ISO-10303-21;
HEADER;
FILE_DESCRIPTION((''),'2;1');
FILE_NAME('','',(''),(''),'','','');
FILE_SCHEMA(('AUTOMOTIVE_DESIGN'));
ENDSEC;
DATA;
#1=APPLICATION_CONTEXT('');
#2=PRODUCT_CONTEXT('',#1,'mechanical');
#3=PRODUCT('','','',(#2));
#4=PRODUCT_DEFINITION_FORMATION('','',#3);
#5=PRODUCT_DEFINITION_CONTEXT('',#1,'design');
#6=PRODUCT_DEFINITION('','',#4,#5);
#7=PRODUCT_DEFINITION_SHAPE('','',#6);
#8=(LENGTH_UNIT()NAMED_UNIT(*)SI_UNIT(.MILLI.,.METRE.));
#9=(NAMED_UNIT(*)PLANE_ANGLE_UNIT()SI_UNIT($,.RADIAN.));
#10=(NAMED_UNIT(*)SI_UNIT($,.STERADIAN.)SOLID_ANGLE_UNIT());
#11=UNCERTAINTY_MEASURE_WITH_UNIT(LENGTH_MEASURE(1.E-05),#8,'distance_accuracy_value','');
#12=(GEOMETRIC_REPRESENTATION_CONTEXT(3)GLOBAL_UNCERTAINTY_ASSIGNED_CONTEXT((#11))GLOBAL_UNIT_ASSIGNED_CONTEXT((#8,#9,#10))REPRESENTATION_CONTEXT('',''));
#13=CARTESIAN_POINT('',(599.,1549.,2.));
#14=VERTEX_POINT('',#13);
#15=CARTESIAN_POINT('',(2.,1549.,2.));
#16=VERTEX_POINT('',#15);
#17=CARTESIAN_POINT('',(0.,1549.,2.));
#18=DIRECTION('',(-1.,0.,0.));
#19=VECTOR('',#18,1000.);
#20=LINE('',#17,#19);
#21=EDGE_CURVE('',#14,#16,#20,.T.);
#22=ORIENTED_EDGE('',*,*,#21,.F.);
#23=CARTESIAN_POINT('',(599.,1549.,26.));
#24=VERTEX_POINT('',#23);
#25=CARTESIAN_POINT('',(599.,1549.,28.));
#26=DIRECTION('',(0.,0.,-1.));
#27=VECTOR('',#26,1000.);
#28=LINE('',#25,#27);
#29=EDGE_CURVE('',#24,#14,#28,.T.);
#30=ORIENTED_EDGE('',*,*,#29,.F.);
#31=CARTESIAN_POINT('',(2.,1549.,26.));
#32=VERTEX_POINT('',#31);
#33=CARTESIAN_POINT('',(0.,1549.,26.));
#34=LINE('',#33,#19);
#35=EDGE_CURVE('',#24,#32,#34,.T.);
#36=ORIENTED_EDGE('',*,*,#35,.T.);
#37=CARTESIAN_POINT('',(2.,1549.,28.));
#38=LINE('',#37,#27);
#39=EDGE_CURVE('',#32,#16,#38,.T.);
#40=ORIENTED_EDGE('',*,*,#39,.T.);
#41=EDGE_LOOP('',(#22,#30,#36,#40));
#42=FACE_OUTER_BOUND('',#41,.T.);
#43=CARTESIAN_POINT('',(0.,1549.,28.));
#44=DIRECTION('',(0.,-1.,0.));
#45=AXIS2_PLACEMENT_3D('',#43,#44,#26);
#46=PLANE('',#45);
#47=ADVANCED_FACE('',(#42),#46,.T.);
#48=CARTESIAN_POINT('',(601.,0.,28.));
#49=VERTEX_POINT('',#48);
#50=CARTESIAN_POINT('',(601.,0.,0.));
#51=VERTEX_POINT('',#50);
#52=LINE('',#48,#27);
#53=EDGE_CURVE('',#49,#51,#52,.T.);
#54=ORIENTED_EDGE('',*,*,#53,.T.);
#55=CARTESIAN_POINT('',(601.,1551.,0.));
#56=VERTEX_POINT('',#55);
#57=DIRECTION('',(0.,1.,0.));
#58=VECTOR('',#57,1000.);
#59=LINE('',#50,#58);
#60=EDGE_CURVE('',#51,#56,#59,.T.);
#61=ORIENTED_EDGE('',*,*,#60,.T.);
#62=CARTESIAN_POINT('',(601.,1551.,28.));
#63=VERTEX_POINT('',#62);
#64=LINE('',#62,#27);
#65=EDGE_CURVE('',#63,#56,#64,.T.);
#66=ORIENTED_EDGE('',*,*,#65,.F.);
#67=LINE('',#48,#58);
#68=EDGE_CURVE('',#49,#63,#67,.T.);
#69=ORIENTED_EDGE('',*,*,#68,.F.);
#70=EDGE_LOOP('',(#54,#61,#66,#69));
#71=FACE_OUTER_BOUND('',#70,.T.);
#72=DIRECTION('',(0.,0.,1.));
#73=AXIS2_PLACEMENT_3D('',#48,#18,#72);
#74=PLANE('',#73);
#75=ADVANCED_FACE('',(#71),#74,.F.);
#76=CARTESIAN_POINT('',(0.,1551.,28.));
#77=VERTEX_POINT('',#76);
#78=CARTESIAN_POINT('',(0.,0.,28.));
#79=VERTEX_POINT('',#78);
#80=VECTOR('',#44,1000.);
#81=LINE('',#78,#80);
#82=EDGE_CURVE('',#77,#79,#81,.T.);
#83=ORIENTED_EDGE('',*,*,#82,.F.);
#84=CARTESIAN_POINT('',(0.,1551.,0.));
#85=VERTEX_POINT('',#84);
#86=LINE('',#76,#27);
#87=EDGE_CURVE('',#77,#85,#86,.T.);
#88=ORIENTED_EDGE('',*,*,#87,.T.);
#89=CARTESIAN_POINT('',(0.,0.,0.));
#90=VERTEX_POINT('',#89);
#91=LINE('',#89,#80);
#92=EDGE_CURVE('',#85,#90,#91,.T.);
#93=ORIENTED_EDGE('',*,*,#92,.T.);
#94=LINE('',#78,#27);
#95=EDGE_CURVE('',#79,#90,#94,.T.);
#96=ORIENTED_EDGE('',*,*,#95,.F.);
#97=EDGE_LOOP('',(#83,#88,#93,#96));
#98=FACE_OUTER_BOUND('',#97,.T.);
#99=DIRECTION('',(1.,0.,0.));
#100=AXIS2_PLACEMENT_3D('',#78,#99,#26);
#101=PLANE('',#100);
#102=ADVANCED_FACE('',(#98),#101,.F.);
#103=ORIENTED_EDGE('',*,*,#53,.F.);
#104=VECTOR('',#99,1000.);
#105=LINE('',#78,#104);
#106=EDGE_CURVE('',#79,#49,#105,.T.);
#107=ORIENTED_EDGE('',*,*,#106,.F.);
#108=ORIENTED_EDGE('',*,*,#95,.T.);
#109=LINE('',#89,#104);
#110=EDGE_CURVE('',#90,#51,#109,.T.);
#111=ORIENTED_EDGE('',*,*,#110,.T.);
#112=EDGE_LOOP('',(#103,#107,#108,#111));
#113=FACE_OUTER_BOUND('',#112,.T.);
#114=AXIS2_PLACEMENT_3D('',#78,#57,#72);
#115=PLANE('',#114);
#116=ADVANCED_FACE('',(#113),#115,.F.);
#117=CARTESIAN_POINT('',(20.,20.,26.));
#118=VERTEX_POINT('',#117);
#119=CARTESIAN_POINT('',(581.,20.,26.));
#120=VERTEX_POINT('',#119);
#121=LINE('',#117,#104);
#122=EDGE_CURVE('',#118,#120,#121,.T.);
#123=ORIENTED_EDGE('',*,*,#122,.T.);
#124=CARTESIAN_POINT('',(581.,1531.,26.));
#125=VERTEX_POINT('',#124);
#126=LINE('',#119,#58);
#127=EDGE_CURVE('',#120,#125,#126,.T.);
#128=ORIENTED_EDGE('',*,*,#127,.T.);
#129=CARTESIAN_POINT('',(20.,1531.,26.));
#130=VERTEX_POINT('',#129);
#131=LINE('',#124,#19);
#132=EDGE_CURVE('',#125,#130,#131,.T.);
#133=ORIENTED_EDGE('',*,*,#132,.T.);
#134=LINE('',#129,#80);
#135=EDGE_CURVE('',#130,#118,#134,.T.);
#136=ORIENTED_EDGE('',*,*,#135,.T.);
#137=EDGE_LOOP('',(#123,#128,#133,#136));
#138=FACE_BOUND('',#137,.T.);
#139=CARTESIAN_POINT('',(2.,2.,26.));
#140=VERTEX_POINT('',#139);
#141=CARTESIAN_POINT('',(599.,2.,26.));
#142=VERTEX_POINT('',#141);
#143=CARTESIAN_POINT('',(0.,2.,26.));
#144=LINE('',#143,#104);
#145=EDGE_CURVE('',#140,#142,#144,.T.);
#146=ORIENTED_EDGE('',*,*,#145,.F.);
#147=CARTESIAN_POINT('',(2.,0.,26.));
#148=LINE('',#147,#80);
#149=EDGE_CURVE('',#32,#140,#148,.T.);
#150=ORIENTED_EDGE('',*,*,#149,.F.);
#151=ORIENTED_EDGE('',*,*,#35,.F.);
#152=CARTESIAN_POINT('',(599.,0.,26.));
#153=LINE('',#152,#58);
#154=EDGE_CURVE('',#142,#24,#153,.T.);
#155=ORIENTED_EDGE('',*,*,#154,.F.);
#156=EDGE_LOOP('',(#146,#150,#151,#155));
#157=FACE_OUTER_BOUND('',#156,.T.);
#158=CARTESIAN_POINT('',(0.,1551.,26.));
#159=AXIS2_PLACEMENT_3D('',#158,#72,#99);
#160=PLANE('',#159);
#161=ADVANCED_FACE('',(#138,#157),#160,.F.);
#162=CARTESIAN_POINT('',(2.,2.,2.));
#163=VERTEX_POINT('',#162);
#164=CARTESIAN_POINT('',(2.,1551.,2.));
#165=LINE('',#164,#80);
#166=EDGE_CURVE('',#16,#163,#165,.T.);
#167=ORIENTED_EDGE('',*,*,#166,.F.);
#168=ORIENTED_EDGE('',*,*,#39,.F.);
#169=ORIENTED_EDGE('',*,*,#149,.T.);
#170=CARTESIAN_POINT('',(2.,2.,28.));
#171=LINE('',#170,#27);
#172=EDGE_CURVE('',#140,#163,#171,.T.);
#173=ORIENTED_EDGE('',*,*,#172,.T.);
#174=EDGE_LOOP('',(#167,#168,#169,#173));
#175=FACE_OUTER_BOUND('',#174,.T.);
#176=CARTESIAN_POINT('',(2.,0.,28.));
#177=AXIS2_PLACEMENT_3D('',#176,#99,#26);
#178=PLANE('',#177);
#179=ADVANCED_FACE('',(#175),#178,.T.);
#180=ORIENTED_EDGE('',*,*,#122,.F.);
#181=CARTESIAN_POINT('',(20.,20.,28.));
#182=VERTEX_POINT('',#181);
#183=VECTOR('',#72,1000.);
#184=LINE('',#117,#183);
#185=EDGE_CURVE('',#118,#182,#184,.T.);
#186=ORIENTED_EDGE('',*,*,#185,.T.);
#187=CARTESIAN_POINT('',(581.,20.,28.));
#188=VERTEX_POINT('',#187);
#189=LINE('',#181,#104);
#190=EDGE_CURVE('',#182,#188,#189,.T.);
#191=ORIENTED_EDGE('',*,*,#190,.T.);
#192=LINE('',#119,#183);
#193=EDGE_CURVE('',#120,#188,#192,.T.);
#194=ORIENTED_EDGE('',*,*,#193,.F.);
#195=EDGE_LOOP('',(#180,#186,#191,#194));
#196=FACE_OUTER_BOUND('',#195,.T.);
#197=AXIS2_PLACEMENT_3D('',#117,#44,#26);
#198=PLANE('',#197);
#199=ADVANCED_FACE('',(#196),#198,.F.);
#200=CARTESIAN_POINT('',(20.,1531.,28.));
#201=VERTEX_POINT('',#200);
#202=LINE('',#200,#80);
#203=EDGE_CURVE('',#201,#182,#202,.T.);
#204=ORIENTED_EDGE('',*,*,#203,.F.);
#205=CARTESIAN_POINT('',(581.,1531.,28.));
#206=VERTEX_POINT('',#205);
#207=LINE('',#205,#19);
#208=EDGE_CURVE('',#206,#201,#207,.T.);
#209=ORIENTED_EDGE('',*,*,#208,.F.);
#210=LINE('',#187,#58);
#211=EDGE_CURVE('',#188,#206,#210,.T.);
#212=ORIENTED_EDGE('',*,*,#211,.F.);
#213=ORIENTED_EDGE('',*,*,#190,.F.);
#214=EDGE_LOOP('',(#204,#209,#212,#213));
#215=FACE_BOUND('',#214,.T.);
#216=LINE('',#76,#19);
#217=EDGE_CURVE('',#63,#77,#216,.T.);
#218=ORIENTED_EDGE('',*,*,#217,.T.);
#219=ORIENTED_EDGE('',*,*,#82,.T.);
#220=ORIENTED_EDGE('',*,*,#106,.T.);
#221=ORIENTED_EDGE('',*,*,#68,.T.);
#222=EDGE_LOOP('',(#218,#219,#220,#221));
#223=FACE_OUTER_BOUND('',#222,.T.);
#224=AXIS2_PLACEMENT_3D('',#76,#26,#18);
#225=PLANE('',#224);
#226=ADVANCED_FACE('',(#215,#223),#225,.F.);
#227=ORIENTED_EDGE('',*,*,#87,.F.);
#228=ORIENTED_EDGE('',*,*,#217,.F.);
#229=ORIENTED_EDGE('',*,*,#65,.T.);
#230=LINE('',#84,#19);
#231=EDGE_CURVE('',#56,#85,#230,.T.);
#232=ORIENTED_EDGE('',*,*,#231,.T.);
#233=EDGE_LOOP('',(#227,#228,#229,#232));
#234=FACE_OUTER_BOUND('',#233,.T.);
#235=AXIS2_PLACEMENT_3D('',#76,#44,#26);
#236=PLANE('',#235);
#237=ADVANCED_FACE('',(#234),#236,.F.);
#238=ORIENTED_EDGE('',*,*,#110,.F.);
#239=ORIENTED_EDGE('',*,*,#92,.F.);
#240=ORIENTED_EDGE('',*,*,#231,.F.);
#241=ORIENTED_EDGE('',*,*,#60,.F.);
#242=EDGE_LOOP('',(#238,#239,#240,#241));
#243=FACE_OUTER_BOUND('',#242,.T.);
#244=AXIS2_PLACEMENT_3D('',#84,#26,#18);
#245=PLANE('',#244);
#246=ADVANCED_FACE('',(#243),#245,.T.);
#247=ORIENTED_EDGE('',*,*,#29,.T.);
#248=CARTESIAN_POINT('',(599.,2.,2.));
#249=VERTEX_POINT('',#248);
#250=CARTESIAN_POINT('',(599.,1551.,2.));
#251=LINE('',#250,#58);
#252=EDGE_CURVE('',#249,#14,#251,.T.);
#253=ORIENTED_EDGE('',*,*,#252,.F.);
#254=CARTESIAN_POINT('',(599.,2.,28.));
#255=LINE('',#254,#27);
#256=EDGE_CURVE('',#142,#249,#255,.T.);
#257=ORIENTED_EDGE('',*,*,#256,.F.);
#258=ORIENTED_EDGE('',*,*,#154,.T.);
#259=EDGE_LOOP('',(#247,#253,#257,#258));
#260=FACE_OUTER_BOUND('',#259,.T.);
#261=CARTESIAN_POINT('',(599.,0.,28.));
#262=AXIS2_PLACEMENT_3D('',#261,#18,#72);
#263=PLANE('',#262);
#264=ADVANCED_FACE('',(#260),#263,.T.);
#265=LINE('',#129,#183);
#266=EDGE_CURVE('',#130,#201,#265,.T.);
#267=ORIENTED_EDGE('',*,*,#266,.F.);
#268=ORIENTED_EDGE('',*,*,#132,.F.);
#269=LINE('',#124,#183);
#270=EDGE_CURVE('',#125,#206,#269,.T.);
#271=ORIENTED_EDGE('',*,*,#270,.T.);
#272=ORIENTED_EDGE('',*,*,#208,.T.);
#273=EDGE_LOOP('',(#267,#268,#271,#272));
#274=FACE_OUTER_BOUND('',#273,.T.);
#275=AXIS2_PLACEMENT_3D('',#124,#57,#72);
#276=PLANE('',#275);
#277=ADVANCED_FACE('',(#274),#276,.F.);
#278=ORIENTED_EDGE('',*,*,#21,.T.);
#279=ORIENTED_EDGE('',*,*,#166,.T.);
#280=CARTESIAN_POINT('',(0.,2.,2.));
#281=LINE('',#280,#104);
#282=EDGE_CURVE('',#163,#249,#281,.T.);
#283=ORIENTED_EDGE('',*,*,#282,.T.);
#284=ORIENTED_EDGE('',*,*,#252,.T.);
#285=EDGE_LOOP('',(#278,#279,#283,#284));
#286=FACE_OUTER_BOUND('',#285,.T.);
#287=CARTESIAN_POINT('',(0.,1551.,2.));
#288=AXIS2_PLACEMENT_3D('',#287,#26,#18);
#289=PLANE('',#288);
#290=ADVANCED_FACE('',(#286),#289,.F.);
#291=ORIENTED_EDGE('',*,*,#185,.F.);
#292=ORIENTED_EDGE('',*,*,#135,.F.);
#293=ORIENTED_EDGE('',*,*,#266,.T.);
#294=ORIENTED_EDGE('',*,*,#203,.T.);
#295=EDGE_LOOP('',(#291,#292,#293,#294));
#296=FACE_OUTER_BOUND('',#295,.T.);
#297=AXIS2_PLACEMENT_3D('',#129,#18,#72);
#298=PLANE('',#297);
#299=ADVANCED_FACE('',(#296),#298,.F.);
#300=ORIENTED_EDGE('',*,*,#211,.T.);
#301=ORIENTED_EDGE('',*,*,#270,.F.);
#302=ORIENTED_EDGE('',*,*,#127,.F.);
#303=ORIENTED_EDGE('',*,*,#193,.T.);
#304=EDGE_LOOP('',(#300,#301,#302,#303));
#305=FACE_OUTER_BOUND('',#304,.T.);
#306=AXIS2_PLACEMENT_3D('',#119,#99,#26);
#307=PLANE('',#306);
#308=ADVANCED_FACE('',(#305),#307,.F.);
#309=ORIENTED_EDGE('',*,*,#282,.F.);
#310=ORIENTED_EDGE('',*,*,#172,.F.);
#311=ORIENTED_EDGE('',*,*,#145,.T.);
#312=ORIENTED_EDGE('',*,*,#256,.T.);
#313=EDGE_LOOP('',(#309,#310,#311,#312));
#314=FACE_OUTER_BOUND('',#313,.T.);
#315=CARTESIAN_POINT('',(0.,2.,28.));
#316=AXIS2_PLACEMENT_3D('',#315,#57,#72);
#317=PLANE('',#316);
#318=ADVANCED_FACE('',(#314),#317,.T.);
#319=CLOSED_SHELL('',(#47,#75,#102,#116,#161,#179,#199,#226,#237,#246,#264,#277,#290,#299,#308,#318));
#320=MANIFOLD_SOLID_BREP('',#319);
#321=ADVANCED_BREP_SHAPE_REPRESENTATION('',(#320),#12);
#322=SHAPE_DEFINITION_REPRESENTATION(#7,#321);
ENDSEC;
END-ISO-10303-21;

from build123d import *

# Parameters (mm, degrees)
SKETCH_1_W      = 601
SKETCH_1_H      = 1551
EXTRUDE_1_DEPTH = 28
SHELL_1_T       = -2
SKETCH_2_W      = 601
SKETCH_2_H      = 1551
SKETCH_2_W_2    = 561
SKETCH_2_H_2    = 1511
EXTRUDE_2_DEPTH = 2


with BuildPart() as part:
    # 草图1 → 凸台-拉伸1 (new body)
    with BuildSketch(Plane.XY):
        with Locations((300.5, 775.5)):
            Rectangle(SKETCH_1_W, SKETCH_1_H)
    extrude(amount=EXTRUDE_1_DEPTH)

    # 抽壳1
    shell_1_openings = [part.faces().sort_by_distance(p)[0] for p in [
        (300.5, 775.5, 28),
    ]]
    offset(amount=SHELL_1_T, openings=shell_1_openings, kind=Kind.INTERSECTION)

    # 草图2 → 凸台-拉伸2 (add)
    with BuildSketch(Plane.XY.offset(28)):
        with Locations((300.5, 775.5)):
            Rectangle(SKETCH_2_W, SKETCH_2_H)
        with Locations((300.5, 775.5)):
            Rectangle(SKETCH_2_W_2, SKETCH_2_H_2, mode=Mode.SUBTRACT)
    extrude(amount=-EXTRUDE_2_DEPTH)


solid = part.part
